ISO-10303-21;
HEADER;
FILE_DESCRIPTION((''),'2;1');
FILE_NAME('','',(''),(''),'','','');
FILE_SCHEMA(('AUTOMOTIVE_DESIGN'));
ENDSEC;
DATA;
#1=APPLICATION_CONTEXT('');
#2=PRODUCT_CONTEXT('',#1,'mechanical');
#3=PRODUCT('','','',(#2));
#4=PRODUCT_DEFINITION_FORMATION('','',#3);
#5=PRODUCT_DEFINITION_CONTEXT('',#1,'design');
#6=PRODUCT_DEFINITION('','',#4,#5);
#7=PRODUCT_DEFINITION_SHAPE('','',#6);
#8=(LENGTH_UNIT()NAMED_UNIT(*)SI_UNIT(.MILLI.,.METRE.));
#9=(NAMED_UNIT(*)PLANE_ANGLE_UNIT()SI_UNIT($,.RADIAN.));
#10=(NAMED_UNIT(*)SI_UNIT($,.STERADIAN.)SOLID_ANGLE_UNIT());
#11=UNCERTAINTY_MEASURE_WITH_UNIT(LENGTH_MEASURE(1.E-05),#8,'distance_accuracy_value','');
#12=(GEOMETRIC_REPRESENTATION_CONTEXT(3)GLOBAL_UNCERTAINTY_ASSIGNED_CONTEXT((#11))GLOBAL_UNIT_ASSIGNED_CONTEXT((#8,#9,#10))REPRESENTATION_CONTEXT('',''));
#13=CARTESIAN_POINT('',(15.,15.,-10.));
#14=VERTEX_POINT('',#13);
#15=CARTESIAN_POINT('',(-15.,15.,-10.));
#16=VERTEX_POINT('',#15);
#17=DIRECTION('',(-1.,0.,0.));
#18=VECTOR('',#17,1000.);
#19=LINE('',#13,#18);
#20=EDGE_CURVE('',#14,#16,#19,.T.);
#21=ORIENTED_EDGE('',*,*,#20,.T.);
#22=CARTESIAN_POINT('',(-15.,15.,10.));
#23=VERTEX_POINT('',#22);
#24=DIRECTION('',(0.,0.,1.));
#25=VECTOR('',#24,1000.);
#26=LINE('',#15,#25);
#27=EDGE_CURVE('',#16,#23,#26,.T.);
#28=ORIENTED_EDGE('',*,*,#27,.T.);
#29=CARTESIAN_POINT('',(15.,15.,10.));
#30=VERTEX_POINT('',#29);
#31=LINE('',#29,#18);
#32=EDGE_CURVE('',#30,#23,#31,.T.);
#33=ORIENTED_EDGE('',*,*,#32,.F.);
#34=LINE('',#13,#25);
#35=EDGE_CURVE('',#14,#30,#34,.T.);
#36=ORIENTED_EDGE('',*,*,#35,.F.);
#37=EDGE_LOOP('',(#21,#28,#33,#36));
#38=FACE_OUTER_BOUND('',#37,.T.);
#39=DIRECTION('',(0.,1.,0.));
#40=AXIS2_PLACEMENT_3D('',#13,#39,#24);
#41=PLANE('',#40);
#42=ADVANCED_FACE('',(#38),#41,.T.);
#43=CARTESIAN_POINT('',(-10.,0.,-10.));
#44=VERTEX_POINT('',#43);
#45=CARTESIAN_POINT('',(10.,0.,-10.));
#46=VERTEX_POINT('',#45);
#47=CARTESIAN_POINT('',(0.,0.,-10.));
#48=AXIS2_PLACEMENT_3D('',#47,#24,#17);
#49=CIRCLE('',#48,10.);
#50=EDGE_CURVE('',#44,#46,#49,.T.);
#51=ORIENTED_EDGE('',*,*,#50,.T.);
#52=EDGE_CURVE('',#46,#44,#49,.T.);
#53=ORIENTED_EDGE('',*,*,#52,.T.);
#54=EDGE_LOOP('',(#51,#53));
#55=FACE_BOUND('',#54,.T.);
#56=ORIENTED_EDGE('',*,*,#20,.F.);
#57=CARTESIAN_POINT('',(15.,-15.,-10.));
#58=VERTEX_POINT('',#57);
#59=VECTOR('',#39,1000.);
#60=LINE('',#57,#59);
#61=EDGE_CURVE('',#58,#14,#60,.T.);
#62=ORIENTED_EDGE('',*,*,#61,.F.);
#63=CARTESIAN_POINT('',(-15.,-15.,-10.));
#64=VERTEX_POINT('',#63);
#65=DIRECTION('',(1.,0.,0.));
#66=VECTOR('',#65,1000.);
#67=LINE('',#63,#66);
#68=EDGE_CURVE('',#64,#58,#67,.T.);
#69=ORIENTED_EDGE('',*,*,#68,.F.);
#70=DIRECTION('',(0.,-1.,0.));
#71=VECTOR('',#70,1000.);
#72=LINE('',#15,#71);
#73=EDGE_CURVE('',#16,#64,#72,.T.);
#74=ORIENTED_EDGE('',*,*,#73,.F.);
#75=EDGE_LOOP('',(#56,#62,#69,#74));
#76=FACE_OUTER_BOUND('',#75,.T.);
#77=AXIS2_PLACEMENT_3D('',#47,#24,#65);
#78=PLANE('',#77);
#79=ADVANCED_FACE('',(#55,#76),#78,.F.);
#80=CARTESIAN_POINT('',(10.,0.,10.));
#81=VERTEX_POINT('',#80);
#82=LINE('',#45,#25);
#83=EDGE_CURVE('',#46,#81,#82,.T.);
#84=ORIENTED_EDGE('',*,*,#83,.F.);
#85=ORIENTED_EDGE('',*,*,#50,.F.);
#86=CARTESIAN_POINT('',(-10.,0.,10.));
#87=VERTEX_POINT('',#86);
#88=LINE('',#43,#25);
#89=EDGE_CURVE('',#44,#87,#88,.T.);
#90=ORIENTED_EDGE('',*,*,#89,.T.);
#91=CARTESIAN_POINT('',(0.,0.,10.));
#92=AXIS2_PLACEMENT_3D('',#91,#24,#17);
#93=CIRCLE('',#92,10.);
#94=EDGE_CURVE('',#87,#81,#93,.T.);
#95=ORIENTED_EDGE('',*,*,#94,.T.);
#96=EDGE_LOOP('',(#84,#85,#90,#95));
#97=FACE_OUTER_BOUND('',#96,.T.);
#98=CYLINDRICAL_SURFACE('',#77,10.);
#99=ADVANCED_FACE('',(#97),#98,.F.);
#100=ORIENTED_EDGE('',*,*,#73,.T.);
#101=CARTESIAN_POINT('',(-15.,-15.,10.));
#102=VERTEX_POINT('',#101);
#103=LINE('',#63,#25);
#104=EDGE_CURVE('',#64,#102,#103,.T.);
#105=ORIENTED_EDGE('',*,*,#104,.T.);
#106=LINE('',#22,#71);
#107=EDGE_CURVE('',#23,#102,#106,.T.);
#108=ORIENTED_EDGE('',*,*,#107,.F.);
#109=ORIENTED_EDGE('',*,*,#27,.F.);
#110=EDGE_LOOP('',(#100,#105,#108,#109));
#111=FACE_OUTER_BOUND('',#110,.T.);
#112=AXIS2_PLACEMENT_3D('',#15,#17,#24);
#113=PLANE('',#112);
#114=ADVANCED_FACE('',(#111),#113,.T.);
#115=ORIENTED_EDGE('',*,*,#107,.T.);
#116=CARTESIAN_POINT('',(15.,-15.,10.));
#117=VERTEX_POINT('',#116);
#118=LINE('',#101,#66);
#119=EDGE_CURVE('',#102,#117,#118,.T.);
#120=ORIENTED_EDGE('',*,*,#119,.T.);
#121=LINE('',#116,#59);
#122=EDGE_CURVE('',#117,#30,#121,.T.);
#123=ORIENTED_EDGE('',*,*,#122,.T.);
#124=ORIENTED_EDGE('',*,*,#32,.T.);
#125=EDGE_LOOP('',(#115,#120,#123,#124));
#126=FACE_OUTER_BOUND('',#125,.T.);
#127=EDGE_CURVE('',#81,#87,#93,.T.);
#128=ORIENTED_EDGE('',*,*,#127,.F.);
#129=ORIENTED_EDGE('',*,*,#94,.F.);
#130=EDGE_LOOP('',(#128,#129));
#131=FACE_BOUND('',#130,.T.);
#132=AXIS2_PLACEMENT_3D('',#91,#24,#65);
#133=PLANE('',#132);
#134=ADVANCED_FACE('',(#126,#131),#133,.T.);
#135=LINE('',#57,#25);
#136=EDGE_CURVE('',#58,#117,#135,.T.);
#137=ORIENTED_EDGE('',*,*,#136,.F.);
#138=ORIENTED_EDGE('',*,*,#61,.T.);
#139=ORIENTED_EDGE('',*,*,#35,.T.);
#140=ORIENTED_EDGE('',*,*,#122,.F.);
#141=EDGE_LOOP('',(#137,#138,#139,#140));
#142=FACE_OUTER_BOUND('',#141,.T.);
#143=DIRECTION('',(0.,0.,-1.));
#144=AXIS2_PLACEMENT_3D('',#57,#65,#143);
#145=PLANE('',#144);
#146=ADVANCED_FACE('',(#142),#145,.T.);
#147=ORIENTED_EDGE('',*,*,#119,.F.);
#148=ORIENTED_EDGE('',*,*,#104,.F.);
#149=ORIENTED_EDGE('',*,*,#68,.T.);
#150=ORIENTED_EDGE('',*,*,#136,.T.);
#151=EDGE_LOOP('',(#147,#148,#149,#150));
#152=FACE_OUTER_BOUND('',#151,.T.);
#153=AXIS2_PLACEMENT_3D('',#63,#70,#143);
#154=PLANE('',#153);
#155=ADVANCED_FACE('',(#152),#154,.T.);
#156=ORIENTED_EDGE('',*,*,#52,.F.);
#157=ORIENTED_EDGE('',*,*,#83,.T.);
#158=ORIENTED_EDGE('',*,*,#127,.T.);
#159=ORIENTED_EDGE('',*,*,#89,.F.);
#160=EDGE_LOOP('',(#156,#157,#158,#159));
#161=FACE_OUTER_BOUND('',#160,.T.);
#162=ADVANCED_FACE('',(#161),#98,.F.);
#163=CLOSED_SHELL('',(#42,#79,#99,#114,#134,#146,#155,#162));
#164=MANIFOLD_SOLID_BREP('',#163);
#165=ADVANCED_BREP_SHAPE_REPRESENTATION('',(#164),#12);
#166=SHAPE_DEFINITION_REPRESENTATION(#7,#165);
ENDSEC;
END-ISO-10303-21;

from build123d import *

# Parameters (mm, degrees)
SKETCH1_W           = 30
SKETCH1_H           = 30
SKETCH1_R           = 10
BOSS_EXTRUDE1_DEPTH = 20


with BuildPart() as part:
    # Sketch1 → Boss-Extrude1 (new body)
    with BuildSketch(Plane.XY.offset(10)):
        Rectangle(SKETCH1_W, SKETCH1_H)
        with Locations(Location((0, 0, 0), (0, 0, 180))):
            Circle(SKETCH1_R, mode=Mode.SUBTRACT)
    extrude(amount=-BOSS_EXTRUDE1_DEPTH)


solid = part.part
